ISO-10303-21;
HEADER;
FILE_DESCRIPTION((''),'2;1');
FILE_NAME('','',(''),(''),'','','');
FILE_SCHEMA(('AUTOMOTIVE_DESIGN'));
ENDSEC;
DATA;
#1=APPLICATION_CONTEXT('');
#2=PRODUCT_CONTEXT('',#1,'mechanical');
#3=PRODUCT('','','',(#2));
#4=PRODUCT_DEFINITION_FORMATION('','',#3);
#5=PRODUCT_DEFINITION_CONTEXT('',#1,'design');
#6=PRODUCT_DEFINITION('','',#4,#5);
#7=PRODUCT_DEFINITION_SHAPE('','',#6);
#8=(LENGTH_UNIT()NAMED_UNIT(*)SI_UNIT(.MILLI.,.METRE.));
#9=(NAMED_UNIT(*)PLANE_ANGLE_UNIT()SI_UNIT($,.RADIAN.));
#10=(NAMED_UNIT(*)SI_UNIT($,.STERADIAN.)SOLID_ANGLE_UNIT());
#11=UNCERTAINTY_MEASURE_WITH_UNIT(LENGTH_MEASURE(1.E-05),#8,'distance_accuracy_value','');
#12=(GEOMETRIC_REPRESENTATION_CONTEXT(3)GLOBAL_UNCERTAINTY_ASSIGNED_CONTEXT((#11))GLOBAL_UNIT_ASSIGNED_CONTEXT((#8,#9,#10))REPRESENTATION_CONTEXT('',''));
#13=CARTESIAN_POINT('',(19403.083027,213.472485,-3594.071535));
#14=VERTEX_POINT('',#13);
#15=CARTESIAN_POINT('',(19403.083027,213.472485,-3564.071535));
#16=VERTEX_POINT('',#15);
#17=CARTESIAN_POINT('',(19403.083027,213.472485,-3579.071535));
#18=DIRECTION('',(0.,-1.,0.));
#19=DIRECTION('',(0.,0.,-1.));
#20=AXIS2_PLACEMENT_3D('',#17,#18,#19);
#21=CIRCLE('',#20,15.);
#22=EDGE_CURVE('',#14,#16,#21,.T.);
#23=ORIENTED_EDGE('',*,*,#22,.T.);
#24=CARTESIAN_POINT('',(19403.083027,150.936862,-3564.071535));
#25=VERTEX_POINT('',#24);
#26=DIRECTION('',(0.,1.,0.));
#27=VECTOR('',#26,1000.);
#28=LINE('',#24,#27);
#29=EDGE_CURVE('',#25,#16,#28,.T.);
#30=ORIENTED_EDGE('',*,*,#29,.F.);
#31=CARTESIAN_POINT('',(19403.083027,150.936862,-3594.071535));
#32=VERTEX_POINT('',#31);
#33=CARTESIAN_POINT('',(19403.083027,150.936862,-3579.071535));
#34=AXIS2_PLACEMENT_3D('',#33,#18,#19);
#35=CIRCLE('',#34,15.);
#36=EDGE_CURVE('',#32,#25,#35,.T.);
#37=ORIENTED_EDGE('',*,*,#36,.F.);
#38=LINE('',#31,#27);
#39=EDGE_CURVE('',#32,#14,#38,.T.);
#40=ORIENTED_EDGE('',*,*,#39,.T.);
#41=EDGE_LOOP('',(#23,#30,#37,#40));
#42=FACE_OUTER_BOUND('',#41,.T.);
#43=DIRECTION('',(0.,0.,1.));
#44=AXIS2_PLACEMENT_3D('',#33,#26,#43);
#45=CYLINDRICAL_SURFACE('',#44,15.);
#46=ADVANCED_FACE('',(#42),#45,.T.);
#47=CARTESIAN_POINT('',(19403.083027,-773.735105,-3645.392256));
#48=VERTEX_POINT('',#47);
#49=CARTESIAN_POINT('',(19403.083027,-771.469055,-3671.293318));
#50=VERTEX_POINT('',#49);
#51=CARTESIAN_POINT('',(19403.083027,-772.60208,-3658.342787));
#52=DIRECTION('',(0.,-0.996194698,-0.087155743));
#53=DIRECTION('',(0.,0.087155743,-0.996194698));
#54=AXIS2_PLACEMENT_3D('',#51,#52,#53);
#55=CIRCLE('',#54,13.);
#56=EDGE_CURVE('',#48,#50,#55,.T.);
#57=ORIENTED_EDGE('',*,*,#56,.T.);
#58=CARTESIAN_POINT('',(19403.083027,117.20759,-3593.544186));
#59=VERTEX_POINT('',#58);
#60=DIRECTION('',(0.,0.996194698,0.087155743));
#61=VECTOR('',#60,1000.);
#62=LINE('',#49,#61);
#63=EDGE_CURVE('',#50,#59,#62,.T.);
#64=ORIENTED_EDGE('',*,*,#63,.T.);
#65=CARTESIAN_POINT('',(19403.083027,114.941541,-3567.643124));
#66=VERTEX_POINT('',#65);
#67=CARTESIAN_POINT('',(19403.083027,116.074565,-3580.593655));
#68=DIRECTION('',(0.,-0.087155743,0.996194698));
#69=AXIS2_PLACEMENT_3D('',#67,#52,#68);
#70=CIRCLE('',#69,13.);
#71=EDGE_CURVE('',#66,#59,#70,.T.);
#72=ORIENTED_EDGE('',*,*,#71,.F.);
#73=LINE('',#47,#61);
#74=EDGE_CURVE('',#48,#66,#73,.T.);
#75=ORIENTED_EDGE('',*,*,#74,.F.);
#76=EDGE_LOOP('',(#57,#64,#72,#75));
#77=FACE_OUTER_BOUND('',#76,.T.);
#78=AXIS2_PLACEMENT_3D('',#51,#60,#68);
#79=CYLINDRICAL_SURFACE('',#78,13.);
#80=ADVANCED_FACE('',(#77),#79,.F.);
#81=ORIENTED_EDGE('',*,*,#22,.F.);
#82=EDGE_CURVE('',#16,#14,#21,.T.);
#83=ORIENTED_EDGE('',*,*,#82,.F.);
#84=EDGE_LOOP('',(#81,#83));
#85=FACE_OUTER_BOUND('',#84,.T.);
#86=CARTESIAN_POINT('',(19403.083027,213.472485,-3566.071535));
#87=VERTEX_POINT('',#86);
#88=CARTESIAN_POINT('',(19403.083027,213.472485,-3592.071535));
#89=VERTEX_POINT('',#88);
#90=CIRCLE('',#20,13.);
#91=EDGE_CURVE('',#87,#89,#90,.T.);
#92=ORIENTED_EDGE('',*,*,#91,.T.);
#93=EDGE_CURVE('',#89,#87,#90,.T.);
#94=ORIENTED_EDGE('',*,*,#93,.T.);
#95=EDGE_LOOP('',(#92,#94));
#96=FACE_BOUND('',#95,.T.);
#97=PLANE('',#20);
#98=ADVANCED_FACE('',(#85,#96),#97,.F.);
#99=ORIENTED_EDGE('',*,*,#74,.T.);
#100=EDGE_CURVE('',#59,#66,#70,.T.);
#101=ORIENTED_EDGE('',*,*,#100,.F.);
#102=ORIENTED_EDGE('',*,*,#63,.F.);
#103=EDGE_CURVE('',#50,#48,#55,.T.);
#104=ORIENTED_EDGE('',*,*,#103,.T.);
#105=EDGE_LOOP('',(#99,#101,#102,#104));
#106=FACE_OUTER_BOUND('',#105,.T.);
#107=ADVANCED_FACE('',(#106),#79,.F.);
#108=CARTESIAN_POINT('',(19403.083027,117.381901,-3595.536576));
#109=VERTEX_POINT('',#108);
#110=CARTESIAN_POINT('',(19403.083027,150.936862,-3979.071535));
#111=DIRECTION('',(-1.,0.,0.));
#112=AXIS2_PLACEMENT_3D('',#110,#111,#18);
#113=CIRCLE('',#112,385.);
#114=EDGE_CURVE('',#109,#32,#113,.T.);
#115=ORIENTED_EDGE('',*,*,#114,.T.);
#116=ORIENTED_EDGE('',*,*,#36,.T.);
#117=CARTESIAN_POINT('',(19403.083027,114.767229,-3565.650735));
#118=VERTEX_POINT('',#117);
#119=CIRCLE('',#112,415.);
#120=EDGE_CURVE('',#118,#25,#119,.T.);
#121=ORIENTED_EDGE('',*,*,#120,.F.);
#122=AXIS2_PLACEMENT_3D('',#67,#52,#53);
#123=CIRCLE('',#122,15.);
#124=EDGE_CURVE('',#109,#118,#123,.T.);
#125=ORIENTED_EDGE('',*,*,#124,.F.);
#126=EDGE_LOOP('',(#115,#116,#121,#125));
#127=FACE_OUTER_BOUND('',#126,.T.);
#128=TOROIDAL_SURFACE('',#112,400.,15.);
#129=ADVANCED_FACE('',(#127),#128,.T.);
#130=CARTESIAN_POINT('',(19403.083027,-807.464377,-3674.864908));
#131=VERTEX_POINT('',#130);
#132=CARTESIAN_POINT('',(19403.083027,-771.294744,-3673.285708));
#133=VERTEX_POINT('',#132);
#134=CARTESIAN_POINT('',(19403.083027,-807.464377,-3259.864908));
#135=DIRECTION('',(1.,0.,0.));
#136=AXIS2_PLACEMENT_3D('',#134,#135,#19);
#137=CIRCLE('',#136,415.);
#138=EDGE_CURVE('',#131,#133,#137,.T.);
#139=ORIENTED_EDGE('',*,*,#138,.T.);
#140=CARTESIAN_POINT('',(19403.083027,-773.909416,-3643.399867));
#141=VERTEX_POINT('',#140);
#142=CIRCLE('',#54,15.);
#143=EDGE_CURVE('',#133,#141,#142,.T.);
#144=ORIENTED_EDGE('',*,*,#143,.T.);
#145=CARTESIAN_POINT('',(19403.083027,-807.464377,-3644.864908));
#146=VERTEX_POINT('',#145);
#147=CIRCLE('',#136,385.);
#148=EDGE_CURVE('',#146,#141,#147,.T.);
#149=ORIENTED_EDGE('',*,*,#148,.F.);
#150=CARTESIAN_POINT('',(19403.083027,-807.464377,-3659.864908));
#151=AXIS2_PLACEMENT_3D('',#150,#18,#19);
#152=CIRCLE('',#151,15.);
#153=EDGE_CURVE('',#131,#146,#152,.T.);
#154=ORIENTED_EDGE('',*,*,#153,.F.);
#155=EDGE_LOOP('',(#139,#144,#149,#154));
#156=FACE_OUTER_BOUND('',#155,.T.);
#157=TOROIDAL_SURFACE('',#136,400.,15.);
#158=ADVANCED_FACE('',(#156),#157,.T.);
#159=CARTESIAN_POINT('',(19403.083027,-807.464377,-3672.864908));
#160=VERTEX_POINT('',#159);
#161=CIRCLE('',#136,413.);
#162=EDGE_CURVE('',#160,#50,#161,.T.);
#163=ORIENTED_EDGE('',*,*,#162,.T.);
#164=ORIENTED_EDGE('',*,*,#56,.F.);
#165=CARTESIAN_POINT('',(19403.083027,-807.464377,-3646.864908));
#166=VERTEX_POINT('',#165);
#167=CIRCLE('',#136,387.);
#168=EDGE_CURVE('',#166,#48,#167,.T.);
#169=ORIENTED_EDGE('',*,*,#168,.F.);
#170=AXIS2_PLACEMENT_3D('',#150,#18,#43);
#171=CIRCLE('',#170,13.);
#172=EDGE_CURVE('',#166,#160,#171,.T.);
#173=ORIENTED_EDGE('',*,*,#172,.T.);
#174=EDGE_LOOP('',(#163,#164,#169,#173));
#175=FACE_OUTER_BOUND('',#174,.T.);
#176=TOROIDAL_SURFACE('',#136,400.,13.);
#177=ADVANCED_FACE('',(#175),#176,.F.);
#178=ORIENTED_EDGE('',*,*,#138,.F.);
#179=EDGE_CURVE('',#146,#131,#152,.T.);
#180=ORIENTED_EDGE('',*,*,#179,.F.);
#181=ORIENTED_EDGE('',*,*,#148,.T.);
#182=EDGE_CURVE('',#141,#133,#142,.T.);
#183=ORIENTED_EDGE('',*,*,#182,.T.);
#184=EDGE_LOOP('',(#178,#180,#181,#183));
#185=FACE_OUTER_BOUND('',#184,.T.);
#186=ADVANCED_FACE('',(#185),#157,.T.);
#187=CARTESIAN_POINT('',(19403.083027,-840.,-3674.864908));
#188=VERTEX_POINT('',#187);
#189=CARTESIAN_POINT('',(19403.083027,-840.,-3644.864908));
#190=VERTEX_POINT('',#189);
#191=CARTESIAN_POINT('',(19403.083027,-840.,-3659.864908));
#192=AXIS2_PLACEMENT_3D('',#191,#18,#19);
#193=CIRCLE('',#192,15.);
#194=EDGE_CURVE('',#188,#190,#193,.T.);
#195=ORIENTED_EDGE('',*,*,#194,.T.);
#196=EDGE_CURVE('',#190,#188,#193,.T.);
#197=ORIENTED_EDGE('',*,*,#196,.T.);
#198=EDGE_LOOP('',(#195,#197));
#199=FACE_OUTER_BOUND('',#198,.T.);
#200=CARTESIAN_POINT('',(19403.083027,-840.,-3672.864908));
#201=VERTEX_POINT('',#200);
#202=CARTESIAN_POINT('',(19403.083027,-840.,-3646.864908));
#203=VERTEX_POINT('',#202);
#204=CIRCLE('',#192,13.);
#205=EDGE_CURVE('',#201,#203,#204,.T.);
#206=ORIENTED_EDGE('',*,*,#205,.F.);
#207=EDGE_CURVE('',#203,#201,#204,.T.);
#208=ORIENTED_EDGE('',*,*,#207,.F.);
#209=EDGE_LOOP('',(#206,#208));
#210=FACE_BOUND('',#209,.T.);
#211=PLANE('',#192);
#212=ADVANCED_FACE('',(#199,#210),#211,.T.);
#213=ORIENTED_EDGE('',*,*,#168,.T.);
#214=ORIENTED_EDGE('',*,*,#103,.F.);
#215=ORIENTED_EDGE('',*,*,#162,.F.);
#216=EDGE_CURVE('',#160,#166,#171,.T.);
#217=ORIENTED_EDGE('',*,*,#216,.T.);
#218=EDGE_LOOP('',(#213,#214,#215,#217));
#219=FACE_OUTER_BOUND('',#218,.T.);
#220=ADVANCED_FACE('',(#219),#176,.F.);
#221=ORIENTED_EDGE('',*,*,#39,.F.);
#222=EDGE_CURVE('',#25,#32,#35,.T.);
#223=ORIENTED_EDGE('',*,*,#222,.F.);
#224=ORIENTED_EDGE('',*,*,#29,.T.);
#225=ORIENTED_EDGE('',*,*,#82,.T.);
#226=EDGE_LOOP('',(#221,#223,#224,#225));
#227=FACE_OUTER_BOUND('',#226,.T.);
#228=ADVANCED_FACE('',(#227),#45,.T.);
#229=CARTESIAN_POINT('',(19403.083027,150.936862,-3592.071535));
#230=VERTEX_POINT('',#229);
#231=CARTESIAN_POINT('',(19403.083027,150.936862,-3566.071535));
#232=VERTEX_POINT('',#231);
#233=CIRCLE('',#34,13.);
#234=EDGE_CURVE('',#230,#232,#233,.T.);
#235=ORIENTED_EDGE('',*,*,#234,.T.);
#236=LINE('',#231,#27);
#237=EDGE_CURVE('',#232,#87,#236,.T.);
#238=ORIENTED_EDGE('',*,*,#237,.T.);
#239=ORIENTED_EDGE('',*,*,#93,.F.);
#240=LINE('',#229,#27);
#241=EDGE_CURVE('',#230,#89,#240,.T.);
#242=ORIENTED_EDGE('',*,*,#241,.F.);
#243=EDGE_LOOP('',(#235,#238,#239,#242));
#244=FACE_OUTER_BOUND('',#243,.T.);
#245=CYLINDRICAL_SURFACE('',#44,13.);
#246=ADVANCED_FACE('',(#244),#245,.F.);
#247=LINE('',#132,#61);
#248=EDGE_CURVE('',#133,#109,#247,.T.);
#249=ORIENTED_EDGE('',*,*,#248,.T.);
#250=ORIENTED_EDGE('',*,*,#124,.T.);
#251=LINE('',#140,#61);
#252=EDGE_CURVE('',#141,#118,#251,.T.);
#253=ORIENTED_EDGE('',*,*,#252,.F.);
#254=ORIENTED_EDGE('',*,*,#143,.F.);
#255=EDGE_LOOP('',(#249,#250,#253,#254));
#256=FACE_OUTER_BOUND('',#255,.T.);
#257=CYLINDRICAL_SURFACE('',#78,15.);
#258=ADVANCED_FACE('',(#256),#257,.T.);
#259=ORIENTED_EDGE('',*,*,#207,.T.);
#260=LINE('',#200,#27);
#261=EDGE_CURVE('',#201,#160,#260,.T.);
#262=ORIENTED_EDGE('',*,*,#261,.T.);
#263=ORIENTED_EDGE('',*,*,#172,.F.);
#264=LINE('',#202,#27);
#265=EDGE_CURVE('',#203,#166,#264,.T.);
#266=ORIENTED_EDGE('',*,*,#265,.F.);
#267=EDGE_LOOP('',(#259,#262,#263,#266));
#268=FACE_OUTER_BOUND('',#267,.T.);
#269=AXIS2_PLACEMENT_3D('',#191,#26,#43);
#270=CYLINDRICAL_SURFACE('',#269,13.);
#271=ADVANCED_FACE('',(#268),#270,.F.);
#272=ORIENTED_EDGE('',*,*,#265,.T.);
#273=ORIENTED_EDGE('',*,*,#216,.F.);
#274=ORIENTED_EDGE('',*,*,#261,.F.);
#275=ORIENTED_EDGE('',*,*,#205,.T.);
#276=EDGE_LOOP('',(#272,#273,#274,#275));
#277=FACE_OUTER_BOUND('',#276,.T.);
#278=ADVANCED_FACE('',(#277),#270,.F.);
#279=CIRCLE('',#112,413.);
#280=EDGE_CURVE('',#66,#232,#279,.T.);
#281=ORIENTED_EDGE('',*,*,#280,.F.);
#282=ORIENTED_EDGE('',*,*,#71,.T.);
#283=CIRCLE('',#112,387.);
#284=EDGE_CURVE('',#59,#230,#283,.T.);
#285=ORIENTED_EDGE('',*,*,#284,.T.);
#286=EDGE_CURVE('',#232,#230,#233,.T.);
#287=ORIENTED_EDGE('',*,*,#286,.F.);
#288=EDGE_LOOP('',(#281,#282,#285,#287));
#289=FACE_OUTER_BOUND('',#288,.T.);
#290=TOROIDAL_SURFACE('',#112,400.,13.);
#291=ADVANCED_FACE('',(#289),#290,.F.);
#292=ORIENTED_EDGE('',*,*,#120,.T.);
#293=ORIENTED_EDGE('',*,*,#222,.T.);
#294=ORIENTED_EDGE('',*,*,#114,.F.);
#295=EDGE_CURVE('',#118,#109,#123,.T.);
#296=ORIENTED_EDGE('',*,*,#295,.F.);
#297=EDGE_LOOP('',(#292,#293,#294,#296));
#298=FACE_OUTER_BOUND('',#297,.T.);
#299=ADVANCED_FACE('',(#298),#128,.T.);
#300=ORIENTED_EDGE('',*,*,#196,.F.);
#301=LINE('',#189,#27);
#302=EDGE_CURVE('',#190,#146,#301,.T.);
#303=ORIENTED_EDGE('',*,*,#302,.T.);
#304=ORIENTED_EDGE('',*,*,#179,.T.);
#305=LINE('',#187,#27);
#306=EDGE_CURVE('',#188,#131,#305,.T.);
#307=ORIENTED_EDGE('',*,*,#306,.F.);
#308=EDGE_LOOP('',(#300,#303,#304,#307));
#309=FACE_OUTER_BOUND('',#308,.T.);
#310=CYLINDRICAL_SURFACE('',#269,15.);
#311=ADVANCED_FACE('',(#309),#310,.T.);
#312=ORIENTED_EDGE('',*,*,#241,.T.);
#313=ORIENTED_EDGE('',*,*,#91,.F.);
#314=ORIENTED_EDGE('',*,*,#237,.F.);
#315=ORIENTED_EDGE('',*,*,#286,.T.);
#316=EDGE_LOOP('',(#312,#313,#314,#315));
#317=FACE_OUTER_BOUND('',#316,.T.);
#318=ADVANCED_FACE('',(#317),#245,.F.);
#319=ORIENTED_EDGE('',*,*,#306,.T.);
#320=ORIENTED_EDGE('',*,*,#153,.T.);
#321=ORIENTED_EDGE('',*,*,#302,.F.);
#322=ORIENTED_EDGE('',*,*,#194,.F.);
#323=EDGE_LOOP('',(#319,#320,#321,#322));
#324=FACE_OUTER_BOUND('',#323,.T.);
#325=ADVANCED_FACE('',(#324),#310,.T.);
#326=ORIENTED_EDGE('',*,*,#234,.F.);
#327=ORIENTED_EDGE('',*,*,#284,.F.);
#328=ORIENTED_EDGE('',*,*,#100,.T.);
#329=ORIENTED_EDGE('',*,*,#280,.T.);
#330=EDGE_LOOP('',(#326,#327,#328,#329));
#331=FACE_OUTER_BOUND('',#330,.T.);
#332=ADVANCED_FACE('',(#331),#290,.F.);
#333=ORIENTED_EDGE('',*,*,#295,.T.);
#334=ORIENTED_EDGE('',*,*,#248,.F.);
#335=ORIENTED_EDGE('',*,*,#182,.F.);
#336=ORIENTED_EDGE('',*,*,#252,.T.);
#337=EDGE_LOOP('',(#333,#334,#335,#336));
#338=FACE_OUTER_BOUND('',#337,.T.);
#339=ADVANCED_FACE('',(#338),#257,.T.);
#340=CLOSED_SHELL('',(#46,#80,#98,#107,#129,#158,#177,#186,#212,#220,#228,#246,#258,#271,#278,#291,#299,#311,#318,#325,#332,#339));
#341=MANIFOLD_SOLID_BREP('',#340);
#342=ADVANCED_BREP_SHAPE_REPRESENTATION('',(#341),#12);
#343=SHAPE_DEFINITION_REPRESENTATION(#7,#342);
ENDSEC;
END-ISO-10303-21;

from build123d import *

# Parameters (mm, degrees)
SWEEP_THIN1_PROFILE_R   = 15
SWEEP_THIN1_PROFILE_R_2 = 13


with BuildPart() as part:
    # Sweep-Thin1: sweep along a curve in space
    with BuildLine() as sweep_thin1_path:
        Line((19403.083026604, -840, -3659.86490803), (19403.083026604, -807.464377163, -3659.86490803))
        ThreePointArc((19403.083026604, -807.464377163, -3659.86490803), (19403.083026604, -790.016622217, -3659.484196663), (19403.083026604, -772.602080064, -3658.342787267))
        Line((19403.083026604, -772.602080064, -3658.342787267), (19403.083026604, 116.074565195, -3580.593655266))
        ThreePointArc((19403.083026604, 116.074565195, -3580.593655266), (19403.083026604, 133.489107348, -3579.45224587), (19403.083026604, 150.936862294, -3579.071534503))
        Line((19403.083026604, 150.936862294, -3579.071534503), (19403.083026604, 213.472485131, -3579.071534503))
    # Sweep-Thin1 profile (on start of the path) → Sweep-Thin1 (sweep)
    with BuildSketch(Plane(origin=(19403.083026604, -840, -3659.86490803), x_dir=(0, 0, 1), z_dir=(0, 1, 0))):
        Circle(SWEEP_THIN1_PROFILE_R)
        Circle(SWEEP_THIN1_PROFILE_R_2, mode=Mode.SUBTRACT)
    sweep(path=sweep_thin1_path.line)


solid = part.part
